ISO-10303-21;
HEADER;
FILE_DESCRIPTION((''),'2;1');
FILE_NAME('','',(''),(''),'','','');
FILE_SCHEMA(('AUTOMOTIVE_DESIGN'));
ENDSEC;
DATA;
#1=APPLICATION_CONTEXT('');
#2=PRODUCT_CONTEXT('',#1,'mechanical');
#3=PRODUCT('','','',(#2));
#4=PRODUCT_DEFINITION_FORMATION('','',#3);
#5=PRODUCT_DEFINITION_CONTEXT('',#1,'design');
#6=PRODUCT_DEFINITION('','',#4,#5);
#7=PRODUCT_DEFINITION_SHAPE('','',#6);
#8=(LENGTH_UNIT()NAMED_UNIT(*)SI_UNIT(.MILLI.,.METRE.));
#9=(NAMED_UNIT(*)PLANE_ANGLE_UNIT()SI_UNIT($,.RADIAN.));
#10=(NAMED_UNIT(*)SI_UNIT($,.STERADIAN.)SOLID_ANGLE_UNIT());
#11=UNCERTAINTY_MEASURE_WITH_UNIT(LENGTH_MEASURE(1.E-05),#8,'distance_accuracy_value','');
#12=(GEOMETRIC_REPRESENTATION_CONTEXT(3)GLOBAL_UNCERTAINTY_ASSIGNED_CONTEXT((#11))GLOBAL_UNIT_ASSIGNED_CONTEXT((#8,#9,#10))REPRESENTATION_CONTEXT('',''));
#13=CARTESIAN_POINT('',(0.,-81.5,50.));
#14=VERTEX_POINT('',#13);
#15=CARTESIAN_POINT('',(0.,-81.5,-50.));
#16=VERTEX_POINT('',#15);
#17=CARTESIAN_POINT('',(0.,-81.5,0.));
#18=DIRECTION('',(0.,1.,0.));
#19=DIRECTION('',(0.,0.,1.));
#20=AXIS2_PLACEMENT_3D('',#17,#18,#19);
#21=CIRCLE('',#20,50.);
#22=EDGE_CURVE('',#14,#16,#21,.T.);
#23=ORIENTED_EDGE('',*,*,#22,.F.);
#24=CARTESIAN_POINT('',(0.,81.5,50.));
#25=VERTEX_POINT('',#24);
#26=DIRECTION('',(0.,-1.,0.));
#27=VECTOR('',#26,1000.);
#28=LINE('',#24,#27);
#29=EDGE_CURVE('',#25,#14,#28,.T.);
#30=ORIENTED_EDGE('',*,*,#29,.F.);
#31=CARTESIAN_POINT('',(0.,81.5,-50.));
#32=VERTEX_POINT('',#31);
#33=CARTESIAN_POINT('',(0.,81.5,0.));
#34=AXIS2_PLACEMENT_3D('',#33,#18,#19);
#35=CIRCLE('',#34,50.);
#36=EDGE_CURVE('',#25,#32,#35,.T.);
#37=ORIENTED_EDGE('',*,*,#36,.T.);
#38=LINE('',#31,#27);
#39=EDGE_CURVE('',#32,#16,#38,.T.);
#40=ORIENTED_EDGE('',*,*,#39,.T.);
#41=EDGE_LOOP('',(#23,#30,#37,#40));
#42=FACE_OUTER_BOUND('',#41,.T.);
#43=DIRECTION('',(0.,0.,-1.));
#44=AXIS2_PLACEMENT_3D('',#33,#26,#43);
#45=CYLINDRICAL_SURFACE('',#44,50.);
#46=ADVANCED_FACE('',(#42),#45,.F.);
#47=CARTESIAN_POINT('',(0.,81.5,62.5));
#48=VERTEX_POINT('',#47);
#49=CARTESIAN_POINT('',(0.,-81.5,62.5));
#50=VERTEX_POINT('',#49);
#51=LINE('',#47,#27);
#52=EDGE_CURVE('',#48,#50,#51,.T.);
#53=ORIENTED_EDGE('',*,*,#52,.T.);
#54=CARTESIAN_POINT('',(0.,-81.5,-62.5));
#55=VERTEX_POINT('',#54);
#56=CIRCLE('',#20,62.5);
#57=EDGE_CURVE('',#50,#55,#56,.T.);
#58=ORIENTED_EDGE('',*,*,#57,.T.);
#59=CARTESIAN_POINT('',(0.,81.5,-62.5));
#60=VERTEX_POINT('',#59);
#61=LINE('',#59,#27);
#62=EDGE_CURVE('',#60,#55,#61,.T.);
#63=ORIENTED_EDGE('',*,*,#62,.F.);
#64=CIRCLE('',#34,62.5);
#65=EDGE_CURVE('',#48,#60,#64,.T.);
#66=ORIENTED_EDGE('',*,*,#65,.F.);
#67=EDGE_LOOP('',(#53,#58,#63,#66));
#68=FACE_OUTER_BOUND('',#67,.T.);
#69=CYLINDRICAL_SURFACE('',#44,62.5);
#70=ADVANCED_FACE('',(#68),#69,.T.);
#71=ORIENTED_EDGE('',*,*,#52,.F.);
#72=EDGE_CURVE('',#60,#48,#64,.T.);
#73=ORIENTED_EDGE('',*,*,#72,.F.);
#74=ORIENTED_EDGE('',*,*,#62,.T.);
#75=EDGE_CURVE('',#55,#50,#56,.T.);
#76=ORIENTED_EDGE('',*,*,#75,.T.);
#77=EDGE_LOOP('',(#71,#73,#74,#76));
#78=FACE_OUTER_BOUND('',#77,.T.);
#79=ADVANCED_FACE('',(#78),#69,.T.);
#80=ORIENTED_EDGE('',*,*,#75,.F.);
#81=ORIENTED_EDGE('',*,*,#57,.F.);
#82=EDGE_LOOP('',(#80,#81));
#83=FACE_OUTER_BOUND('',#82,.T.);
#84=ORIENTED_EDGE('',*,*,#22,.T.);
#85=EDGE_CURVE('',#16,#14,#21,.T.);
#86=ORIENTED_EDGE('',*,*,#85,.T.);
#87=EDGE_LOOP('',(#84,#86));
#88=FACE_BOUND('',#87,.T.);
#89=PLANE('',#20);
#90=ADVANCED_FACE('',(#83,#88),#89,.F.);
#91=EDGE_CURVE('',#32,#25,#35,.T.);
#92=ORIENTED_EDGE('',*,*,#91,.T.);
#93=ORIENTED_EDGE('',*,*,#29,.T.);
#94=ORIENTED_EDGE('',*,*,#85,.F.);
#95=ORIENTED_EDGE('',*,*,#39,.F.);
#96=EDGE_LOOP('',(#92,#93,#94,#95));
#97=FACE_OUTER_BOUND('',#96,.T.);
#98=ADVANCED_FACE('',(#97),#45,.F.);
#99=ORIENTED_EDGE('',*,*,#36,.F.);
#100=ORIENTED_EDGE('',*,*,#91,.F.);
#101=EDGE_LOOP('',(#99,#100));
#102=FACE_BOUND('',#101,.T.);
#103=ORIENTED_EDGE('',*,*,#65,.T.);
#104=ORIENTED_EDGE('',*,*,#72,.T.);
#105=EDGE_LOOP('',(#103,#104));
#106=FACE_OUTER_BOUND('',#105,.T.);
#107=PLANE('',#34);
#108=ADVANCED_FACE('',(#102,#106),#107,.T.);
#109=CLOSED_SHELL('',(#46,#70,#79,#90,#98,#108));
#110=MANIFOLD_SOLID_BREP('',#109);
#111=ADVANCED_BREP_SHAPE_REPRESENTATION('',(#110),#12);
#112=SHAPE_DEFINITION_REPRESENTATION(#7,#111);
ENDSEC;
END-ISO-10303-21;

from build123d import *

# Parameters (mm, degrees)
TUBE_PROFILE_125_100_R   = 62.5
TUBE_PROFILE_125_100_R_2 = 50
SPACER_TUBE_L163_DEPTH   = 81.5


with BuildPart() as part:
    # Tube Profile Ø125-Ø100 → Spacer Tube L163 (new, symmetric)
    with BuildSketch(Plane(origin=(0, 0, 0), x_dir=(1, 0, 0), z_dir=(0, 1, 0))):
        with Locations(Location((0, 0, 0), (0, 0, 270))):
            Circle(TUBE_PROFILE_125_100_R)
        with Locations(Location((0, 0, 0), (0, 0, 270))):
            Circle(TUBE_PROFILE_125_100_R_2, mode=Mode.SUBTRACT)
    extrude(amount=SPACER_TUBE_L163_DEPTH, both=True)


solid = part.part
